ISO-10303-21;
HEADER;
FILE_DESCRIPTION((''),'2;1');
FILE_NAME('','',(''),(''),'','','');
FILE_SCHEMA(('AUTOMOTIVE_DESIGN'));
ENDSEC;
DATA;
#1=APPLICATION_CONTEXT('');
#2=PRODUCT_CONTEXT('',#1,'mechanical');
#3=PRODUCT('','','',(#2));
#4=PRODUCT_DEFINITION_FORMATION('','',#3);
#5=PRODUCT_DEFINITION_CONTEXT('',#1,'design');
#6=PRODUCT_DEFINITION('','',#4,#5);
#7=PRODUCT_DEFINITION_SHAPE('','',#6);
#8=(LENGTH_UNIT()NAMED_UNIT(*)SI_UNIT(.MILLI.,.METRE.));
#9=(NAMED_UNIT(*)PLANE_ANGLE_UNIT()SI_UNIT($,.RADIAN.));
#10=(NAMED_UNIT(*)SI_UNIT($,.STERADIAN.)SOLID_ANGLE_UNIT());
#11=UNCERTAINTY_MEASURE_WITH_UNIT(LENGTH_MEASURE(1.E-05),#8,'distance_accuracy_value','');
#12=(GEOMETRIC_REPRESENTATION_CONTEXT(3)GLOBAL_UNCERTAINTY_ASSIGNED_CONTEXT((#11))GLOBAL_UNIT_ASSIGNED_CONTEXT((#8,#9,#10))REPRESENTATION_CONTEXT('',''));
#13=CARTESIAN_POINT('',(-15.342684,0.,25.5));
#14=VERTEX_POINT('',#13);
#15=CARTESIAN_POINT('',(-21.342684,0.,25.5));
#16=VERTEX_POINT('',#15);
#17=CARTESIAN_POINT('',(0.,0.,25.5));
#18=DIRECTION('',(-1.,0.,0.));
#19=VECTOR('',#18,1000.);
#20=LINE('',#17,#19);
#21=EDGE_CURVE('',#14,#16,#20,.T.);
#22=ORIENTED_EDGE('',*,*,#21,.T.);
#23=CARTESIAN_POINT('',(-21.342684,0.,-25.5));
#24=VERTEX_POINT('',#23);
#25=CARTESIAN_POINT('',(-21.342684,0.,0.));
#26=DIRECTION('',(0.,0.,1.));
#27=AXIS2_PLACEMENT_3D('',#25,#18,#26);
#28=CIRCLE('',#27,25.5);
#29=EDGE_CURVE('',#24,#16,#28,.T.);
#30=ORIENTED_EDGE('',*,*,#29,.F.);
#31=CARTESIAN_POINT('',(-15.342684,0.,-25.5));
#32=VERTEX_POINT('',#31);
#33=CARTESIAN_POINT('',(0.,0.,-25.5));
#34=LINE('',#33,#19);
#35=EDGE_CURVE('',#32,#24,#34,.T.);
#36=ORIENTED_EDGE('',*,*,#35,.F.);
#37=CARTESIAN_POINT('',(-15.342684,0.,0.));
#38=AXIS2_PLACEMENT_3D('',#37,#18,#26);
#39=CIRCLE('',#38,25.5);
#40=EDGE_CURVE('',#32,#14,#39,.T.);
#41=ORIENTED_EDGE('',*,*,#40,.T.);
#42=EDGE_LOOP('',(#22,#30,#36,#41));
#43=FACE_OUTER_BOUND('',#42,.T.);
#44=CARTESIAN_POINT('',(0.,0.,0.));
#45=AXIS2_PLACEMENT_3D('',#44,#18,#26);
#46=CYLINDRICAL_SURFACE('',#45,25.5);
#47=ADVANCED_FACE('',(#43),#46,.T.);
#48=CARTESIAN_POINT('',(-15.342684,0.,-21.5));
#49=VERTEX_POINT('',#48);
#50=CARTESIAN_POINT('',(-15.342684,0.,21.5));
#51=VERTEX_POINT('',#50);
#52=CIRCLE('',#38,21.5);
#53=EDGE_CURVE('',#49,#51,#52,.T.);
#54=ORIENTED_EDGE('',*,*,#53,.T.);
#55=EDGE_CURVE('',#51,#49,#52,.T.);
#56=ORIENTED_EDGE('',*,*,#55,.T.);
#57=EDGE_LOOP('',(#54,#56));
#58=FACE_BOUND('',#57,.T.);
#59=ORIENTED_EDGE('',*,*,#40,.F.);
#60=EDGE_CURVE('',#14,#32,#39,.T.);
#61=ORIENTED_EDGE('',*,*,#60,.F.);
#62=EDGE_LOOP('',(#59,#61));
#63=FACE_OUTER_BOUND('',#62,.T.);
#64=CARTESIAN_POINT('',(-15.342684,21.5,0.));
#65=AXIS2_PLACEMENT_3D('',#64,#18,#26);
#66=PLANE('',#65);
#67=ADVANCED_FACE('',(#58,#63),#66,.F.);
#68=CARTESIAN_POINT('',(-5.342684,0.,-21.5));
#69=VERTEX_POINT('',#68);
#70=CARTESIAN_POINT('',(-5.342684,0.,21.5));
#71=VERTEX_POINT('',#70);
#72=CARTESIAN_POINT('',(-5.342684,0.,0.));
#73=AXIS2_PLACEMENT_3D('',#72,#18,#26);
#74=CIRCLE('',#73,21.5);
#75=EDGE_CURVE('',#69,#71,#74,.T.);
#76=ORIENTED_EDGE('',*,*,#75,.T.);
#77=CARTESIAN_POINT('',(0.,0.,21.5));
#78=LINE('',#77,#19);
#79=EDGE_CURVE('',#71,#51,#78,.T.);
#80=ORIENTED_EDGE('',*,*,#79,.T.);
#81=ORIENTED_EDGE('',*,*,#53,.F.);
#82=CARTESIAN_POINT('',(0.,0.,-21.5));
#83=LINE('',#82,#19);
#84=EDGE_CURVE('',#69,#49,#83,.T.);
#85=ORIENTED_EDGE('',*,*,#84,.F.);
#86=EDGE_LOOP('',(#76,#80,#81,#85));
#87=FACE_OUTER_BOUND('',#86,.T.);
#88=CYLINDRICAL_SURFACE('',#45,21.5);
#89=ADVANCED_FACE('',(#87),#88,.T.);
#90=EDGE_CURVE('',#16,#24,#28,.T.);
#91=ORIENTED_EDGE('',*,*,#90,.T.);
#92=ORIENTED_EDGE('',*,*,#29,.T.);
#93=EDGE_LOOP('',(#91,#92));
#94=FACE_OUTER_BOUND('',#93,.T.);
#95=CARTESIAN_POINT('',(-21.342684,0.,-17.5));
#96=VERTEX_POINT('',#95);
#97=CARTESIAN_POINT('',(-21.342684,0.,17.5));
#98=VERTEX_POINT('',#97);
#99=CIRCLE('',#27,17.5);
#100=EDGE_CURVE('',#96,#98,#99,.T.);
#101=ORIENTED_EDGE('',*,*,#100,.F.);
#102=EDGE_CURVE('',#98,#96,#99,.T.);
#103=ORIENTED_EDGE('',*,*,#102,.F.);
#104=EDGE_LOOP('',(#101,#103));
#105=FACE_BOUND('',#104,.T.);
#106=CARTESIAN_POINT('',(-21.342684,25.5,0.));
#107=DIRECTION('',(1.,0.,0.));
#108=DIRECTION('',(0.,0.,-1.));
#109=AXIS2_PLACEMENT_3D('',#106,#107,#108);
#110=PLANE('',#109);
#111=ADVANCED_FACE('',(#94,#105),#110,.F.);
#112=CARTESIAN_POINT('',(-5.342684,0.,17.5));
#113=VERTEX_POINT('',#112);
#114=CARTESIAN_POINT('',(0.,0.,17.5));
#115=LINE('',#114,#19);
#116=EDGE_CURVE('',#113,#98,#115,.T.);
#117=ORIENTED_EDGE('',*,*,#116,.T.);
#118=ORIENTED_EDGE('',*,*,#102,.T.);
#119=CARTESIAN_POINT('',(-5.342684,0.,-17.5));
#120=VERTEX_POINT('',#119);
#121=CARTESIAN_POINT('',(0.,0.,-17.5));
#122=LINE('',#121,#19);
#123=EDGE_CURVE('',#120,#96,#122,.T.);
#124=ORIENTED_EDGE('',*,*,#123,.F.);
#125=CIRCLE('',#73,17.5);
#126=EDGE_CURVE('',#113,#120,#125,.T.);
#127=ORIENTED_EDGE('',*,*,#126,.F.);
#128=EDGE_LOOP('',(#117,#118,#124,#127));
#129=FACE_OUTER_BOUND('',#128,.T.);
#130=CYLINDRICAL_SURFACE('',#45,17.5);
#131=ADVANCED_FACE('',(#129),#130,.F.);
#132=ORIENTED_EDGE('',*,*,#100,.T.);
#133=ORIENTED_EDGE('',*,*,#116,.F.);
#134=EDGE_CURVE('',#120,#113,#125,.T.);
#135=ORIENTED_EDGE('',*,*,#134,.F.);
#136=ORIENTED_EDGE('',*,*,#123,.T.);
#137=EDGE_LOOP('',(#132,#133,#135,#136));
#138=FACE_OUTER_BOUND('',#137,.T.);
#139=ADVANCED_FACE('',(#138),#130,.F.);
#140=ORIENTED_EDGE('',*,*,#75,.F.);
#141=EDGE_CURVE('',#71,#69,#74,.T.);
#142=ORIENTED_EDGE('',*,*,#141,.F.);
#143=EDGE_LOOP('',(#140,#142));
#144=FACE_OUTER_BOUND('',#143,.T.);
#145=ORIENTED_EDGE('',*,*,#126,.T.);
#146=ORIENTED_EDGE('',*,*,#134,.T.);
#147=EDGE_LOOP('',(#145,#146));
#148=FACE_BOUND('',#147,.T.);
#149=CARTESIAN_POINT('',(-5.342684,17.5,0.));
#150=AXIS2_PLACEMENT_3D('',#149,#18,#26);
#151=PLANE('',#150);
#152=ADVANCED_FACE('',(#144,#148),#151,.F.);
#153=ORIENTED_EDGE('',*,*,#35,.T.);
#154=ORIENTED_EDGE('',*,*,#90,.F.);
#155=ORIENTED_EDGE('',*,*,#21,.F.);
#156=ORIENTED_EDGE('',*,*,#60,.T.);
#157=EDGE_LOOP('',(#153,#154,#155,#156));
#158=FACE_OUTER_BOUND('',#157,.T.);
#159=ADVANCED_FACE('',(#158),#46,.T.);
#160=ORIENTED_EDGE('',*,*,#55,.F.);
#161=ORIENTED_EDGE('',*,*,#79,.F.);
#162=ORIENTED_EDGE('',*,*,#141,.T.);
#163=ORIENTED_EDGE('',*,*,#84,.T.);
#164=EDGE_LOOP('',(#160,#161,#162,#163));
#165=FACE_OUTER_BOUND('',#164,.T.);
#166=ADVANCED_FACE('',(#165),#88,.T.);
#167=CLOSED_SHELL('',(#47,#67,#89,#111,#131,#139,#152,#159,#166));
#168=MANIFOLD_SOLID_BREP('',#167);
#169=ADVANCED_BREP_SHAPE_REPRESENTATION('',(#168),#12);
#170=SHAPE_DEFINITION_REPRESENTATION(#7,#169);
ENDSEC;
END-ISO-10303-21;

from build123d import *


with BuildPart() as part:
    # Sketch1 → Revolve1 (revolve)
    with BuildSketch(Plane.XY, mode=Mode.PRIVATE) as revolve1_sk:
        Polygon((-17.211842105, 17.5), (-5.342684211, 17.5), (-5.342684211, 21.5), (-15.342684211, 21.5), (-15.342684211, 25.5), (-21.342684211, 25.5), (-21.342684211, 17.5), align=None)
    revolve(revolve1_sk.sketch.rotate(Axis((0, 0, 0), (1, 0, 0)), 90), axis=Axis((0, 0, 0), (1, 0, 0)))


solid = part.part
